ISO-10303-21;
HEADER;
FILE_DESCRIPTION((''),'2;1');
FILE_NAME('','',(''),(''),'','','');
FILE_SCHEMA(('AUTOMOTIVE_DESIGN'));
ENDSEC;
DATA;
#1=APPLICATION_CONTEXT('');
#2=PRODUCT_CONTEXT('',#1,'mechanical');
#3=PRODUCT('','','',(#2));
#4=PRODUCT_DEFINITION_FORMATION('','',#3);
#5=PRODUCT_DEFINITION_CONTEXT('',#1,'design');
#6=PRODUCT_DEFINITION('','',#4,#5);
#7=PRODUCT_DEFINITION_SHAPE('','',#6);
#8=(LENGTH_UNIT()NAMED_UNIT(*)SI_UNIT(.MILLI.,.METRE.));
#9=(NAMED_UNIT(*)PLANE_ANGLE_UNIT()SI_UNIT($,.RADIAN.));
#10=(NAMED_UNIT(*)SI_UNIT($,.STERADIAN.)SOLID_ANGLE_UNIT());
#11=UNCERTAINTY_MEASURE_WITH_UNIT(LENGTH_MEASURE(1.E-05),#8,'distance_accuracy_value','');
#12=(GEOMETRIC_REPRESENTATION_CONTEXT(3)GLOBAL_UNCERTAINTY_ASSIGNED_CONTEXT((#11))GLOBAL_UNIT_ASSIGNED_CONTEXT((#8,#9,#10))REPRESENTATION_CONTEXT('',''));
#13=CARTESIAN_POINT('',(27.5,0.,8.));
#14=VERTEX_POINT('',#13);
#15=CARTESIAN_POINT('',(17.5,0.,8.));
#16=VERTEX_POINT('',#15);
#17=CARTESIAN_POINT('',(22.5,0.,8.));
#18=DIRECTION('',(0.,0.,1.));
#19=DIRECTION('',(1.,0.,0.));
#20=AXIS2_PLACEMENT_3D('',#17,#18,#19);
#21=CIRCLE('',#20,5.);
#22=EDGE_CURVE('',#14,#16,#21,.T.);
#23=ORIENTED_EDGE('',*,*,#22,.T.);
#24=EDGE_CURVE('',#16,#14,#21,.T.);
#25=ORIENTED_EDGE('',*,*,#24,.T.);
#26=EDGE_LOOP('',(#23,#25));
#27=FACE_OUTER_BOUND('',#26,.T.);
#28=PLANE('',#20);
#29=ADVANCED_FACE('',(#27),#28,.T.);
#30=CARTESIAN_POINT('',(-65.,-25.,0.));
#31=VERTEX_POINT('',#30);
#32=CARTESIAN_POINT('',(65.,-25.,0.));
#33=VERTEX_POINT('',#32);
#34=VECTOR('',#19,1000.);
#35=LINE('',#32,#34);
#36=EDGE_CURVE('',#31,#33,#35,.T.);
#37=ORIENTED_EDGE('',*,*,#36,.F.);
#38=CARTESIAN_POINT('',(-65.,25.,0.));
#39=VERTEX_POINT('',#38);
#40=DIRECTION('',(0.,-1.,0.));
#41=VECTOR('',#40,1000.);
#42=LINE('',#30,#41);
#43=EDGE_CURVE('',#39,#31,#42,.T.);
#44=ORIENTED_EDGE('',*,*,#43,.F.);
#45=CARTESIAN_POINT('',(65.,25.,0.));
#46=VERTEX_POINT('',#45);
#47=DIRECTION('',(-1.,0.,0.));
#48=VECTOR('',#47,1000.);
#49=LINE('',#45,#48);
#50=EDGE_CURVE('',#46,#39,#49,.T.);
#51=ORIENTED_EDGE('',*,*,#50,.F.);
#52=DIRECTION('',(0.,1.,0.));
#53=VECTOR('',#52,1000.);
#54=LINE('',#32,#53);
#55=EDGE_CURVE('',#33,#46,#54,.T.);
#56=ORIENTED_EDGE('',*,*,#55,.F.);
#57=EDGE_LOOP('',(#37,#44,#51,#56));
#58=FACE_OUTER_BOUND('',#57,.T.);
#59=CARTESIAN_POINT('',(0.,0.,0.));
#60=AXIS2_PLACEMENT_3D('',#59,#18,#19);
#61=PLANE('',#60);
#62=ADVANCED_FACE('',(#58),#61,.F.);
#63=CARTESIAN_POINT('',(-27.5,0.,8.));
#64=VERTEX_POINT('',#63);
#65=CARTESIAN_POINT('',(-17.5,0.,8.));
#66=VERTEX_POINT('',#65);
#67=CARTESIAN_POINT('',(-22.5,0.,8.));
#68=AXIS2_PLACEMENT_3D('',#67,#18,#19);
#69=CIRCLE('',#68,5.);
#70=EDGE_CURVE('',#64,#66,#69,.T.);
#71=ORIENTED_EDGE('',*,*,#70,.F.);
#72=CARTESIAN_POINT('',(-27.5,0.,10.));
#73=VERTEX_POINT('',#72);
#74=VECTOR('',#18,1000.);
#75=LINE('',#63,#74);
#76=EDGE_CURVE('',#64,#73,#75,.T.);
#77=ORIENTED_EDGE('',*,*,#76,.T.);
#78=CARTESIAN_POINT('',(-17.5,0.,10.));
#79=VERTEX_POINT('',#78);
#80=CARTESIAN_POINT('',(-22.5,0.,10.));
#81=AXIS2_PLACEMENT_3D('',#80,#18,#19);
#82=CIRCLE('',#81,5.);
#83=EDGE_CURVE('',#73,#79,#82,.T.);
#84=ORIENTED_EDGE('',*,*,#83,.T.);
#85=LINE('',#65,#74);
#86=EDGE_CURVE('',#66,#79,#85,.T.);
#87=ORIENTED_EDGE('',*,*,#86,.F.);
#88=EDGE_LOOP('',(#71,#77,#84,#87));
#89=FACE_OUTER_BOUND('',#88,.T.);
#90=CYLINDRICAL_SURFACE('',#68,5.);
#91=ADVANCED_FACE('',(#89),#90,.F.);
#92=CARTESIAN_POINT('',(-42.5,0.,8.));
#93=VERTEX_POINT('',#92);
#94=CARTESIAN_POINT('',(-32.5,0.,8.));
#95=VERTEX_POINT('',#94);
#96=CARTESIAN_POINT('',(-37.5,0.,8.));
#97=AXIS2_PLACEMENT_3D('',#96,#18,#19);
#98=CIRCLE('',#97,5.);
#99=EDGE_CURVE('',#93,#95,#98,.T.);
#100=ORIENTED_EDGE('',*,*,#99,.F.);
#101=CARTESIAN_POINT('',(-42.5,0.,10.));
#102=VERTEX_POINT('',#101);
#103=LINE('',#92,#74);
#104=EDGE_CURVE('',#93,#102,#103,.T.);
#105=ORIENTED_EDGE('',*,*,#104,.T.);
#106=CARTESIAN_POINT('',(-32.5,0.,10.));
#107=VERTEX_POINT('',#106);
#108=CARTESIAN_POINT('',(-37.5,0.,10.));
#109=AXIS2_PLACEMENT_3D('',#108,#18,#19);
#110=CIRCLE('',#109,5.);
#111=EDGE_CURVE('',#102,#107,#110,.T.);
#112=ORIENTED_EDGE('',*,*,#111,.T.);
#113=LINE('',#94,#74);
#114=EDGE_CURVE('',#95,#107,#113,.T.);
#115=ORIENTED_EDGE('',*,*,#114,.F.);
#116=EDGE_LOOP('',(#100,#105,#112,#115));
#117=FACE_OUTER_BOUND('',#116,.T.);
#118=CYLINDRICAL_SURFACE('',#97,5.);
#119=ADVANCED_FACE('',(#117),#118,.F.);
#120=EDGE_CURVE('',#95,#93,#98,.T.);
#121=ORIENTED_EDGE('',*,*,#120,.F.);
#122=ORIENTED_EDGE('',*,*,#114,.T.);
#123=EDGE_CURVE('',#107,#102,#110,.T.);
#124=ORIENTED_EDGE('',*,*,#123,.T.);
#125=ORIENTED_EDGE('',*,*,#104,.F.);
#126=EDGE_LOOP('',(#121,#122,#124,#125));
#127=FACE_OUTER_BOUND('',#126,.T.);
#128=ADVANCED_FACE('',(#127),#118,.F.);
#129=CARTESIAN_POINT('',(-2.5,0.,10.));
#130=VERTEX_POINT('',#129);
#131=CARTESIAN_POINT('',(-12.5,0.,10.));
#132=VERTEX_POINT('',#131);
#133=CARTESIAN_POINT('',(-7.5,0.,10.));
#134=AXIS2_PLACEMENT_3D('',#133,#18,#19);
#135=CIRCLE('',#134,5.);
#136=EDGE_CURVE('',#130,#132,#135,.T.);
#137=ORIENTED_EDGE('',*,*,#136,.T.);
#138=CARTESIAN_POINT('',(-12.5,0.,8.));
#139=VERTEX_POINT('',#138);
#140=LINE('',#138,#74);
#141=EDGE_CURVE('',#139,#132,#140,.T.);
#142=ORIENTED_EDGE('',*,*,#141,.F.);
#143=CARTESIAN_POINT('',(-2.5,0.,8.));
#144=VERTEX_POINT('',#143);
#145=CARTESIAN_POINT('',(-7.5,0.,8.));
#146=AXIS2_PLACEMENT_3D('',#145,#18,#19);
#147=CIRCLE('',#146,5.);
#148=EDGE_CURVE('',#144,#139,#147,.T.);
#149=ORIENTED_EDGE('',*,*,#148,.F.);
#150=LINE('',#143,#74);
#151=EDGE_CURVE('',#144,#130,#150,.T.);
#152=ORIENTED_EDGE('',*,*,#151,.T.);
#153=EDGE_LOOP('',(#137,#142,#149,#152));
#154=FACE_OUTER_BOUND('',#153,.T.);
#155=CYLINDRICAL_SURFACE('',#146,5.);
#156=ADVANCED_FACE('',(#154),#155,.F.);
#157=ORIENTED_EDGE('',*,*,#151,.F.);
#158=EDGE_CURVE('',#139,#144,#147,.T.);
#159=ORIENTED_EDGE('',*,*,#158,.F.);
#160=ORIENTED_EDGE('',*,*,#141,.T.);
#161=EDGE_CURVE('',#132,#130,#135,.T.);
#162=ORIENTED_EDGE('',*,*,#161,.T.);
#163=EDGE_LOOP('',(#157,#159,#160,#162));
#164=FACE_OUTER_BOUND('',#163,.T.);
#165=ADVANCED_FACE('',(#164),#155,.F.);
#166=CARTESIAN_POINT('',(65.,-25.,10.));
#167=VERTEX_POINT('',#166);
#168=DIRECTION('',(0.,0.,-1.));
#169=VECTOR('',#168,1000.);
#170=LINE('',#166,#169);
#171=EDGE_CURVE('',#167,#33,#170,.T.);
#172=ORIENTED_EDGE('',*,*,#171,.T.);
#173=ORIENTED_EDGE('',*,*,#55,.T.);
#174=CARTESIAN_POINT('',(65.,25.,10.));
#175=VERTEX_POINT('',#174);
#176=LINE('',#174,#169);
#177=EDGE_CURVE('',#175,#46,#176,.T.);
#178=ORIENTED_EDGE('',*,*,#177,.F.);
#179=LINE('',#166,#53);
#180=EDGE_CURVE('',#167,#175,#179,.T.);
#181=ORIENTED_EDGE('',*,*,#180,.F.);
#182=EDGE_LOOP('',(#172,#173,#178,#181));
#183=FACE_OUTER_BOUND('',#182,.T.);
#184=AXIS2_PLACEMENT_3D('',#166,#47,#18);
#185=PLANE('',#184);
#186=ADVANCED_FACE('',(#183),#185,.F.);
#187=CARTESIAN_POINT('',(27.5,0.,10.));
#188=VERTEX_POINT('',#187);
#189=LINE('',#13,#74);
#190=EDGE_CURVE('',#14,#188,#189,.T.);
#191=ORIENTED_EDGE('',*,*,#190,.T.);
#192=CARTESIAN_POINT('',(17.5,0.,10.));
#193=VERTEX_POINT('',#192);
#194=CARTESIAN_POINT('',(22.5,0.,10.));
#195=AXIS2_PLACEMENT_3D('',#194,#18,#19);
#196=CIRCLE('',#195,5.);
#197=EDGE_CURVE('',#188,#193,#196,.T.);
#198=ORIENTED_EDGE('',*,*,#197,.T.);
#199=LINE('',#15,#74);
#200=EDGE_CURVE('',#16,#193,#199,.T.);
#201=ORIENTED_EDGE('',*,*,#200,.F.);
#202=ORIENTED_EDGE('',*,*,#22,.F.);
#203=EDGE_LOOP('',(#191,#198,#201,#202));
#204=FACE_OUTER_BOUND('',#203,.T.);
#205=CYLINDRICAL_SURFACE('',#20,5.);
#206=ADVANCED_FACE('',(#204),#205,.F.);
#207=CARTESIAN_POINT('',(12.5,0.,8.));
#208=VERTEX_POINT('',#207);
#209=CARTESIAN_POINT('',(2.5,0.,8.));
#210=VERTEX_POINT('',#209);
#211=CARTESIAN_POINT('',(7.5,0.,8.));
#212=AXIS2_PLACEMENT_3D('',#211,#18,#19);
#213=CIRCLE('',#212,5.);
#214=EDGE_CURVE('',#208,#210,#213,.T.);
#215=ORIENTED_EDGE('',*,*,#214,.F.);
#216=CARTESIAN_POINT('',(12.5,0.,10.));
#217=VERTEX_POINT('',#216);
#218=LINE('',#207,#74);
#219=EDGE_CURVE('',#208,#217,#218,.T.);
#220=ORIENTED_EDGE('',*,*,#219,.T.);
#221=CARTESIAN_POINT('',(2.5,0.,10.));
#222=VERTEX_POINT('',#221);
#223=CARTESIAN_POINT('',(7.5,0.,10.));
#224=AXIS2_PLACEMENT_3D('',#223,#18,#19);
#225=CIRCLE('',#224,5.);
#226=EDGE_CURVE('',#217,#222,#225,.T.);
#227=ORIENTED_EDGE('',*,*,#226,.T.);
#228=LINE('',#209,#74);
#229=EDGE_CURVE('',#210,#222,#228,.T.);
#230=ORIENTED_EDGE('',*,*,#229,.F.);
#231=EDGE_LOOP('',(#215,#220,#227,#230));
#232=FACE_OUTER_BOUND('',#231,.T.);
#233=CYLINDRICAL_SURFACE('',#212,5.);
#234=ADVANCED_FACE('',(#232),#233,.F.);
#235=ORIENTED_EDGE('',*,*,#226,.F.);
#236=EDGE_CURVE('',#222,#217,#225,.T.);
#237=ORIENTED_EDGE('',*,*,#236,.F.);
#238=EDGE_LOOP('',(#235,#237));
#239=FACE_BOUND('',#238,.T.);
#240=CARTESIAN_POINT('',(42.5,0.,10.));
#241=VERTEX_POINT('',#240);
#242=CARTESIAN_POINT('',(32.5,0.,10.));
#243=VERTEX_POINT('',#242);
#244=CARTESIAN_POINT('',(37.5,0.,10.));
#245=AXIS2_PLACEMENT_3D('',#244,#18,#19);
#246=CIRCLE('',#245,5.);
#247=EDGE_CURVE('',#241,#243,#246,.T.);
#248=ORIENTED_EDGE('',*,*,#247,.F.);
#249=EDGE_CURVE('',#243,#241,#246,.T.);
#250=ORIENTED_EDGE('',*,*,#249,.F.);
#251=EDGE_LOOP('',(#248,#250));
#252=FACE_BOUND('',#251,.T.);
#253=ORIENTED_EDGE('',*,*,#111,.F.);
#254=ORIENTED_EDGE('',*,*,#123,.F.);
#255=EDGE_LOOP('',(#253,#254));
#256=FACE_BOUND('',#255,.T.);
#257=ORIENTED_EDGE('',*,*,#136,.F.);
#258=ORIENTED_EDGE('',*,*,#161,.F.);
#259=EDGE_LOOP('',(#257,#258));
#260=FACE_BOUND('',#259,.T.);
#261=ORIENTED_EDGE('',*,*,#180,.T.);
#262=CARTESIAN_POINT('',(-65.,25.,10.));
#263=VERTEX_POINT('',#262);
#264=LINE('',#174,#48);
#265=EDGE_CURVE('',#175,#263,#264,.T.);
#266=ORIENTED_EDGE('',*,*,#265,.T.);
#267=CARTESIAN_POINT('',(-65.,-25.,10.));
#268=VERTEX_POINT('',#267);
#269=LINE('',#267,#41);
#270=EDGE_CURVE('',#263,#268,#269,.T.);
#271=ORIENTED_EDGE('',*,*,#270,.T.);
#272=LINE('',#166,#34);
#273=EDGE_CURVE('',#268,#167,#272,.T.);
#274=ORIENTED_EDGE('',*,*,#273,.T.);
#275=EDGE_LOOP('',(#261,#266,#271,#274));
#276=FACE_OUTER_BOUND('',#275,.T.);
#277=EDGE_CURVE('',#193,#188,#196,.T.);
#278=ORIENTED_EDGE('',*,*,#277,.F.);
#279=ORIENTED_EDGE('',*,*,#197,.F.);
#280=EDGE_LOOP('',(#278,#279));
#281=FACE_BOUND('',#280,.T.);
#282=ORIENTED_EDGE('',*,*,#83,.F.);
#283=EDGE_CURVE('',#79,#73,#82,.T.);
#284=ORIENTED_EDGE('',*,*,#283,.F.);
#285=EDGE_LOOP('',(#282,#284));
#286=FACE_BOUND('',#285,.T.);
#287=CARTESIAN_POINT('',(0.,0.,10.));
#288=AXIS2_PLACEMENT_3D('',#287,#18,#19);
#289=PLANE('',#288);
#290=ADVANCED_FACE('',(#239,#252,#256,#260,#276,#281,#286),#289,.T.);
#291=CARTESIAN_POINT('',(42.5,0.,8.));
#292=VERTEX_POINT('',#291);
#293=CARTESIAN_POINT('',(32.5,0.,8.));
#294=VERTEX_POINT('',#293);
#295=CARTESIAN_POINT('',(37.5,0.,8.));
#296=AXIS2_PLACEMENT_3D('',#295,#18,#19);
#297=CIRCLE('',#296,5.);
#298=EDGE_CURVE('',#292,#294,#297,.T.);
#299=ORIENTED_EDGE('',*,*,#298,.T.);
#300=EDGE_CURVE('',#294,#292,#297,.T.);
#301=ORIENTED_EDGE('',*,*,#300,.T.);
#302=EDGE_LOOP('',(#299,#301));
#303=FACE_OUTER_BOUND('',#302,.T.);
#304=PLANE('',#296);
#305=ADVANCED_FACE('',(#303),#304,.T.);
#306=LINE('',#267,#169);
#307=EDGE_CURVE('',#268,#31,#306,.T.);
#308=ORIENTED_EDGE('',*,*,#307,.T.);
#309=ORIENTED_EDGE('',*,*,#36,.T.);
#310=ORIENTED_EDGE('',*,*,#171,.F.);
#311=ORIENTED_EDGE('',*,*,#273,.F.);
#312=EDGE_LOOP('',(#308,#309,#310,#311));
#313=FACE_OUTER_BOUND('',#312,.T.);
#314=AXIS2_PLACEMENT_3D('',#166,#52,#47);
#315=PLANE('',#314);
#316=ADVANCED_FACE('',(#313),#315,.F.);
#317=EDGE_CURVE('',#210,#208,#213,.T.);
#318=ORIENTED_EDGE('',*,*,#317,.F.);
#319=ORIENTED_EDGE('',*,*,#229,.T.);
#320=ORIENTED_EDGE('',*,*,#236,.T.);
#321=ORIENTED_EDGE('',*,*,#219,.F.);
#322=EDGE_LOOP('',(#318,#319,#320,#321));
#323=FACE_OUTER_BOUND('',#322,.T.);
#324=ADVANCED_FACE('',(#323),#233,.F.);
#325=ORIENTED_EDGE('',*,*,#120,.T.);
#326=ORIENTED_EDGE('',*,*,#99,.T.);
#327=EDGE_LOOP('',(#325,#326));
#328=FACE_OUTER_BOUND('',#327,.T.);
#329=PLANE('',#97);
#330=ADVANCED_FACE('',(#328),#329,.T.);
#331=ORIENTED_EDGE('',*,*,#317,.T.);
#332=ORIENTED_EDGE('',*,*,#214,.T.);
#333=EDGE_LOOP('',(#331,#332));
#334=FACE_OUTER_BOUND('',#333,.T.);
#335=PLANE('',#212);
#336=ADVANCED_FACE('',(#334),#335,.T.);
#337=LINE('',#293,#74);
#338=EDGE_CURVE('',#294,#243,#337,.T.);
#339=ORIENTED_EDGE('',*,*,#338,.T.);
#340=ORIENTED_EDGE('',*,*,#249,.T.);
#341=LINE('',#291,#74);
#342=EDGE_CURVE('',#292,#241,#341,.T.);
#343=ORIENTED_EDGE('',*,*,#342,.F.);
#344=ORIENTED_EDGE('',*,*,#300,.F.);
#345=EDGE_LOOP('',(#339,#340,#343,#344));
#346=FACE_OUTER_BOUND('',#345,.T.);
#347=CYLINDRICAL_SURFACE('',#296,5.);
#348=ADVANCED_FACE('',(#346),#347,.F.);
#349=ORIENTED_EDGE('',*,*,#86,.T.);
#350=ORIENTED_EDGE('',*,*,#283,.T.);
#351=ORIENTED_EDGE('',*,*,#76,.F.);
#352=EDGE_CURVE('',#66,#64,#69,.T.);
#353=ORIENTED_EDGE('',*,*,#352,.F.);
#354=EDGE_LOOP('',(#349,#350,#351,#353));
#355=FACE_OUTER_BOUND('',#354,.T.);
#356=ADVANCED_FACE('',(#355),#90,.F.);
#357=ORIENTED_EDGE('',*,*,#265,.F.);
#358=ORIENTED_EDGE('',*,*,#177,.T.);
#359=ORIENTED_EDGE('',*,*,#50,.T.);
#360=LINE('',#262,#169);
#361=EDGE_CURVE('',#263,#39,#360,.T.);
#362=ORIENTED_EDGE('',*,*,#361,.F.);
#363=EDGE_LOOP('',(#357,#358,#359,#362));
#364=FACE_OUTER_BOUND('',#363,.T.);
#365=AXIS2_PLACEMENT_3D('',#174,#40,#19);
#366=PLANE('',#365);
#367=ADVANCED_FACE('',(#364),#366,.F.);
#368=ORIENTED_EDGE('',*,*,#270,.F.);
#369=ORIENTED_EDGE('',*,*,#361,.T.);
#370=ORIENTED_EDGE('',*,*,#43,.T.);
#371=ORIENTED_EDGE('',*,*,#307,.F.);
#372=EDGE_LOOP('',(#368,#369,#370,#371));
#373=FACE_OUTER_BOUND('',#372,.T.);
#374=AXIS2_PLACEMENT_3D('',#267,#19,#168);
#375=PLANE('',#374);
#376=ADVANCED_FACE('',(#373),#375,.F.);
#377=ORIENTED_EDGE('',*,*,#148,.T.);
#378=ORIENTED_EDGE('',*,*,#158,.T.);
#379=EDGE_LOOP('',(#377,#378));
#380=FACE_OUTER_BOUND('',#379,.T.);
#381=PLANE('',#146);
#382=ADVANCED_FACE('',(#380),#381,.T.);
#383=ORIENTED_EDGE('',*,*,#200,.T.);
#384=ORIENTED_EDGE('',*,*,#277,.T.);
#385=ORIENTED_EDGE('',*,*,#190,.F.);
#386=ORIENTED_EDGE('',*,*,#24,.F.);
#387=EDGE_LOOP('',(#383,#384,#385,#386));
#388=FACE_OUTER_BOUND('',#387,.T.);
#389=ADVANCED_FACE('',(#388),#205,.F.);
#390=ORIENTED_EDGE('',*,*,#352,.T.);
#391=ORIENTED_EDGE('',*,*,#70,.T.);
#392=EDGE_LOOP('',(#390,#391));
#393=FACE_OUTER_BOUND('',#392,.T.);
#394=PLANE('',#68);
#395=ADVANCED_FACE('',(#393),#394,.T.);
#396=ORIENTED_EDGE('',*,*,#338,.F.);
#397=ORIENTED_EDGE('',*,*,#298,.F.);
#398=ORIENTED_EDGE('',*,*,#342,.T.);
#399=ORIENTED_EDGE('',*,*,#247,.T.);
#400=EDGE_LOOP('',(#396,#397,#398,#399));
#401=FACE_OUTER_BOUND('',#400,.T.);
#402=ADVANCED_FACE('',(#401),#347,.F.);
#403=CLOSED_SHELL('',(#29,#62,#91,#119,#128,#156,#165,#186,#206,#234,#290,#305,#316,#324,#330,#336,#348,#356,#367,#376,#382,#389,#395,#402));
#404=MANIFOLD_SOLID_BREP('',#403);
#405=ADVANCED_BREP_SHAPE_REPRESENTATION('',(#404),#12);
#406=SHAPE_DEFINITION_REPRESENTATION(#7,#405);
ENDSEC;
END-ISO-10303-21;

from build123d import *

# Parameters (mm, degrees)
SKETCH1_W           = 130
SKETCH1_H           = 50
BOSS_EXTRUDE1_DEPTH = 10
SKETCH2_R           = 5
CUT_EXTRUDE1_DEPTH  = 2


with BuildPart() as part:
    # Sketch1 → Boss-Extrude1 (new body)
    with BuildSketch(Plane.XY):
        Rectangle(SKETCH1_W, SKETCH1_H)
    extrude(amount=BOSS_EXTRUDE1_DEPTH)

    # Sketch2 → Cut-Extrude1 (cut)
    with BuildSketch(Plane.XY.offset(10)):
        with Locations((-37.5, 0)):
            Circle(SKETCH2_R)
        with Locations((-22.5, 0)):
            Circle(SKETCH2_R)
        with Locations((-7.5, 0)):
            Circle(SKETCH2_R)
        with Locations((7.5, 0)):
            Circle(SKETCH2_R)
        with Locations((22.5, 0)):
            Circle(SKETCH2_R)
        with Locations((37.5, 0)):
            Circle(SKETCH2_R)
    extrude(amount=-CUT_EXTRUDE1_DEPTH, mode=Mode.SUBTRACT)


solid = part.part
